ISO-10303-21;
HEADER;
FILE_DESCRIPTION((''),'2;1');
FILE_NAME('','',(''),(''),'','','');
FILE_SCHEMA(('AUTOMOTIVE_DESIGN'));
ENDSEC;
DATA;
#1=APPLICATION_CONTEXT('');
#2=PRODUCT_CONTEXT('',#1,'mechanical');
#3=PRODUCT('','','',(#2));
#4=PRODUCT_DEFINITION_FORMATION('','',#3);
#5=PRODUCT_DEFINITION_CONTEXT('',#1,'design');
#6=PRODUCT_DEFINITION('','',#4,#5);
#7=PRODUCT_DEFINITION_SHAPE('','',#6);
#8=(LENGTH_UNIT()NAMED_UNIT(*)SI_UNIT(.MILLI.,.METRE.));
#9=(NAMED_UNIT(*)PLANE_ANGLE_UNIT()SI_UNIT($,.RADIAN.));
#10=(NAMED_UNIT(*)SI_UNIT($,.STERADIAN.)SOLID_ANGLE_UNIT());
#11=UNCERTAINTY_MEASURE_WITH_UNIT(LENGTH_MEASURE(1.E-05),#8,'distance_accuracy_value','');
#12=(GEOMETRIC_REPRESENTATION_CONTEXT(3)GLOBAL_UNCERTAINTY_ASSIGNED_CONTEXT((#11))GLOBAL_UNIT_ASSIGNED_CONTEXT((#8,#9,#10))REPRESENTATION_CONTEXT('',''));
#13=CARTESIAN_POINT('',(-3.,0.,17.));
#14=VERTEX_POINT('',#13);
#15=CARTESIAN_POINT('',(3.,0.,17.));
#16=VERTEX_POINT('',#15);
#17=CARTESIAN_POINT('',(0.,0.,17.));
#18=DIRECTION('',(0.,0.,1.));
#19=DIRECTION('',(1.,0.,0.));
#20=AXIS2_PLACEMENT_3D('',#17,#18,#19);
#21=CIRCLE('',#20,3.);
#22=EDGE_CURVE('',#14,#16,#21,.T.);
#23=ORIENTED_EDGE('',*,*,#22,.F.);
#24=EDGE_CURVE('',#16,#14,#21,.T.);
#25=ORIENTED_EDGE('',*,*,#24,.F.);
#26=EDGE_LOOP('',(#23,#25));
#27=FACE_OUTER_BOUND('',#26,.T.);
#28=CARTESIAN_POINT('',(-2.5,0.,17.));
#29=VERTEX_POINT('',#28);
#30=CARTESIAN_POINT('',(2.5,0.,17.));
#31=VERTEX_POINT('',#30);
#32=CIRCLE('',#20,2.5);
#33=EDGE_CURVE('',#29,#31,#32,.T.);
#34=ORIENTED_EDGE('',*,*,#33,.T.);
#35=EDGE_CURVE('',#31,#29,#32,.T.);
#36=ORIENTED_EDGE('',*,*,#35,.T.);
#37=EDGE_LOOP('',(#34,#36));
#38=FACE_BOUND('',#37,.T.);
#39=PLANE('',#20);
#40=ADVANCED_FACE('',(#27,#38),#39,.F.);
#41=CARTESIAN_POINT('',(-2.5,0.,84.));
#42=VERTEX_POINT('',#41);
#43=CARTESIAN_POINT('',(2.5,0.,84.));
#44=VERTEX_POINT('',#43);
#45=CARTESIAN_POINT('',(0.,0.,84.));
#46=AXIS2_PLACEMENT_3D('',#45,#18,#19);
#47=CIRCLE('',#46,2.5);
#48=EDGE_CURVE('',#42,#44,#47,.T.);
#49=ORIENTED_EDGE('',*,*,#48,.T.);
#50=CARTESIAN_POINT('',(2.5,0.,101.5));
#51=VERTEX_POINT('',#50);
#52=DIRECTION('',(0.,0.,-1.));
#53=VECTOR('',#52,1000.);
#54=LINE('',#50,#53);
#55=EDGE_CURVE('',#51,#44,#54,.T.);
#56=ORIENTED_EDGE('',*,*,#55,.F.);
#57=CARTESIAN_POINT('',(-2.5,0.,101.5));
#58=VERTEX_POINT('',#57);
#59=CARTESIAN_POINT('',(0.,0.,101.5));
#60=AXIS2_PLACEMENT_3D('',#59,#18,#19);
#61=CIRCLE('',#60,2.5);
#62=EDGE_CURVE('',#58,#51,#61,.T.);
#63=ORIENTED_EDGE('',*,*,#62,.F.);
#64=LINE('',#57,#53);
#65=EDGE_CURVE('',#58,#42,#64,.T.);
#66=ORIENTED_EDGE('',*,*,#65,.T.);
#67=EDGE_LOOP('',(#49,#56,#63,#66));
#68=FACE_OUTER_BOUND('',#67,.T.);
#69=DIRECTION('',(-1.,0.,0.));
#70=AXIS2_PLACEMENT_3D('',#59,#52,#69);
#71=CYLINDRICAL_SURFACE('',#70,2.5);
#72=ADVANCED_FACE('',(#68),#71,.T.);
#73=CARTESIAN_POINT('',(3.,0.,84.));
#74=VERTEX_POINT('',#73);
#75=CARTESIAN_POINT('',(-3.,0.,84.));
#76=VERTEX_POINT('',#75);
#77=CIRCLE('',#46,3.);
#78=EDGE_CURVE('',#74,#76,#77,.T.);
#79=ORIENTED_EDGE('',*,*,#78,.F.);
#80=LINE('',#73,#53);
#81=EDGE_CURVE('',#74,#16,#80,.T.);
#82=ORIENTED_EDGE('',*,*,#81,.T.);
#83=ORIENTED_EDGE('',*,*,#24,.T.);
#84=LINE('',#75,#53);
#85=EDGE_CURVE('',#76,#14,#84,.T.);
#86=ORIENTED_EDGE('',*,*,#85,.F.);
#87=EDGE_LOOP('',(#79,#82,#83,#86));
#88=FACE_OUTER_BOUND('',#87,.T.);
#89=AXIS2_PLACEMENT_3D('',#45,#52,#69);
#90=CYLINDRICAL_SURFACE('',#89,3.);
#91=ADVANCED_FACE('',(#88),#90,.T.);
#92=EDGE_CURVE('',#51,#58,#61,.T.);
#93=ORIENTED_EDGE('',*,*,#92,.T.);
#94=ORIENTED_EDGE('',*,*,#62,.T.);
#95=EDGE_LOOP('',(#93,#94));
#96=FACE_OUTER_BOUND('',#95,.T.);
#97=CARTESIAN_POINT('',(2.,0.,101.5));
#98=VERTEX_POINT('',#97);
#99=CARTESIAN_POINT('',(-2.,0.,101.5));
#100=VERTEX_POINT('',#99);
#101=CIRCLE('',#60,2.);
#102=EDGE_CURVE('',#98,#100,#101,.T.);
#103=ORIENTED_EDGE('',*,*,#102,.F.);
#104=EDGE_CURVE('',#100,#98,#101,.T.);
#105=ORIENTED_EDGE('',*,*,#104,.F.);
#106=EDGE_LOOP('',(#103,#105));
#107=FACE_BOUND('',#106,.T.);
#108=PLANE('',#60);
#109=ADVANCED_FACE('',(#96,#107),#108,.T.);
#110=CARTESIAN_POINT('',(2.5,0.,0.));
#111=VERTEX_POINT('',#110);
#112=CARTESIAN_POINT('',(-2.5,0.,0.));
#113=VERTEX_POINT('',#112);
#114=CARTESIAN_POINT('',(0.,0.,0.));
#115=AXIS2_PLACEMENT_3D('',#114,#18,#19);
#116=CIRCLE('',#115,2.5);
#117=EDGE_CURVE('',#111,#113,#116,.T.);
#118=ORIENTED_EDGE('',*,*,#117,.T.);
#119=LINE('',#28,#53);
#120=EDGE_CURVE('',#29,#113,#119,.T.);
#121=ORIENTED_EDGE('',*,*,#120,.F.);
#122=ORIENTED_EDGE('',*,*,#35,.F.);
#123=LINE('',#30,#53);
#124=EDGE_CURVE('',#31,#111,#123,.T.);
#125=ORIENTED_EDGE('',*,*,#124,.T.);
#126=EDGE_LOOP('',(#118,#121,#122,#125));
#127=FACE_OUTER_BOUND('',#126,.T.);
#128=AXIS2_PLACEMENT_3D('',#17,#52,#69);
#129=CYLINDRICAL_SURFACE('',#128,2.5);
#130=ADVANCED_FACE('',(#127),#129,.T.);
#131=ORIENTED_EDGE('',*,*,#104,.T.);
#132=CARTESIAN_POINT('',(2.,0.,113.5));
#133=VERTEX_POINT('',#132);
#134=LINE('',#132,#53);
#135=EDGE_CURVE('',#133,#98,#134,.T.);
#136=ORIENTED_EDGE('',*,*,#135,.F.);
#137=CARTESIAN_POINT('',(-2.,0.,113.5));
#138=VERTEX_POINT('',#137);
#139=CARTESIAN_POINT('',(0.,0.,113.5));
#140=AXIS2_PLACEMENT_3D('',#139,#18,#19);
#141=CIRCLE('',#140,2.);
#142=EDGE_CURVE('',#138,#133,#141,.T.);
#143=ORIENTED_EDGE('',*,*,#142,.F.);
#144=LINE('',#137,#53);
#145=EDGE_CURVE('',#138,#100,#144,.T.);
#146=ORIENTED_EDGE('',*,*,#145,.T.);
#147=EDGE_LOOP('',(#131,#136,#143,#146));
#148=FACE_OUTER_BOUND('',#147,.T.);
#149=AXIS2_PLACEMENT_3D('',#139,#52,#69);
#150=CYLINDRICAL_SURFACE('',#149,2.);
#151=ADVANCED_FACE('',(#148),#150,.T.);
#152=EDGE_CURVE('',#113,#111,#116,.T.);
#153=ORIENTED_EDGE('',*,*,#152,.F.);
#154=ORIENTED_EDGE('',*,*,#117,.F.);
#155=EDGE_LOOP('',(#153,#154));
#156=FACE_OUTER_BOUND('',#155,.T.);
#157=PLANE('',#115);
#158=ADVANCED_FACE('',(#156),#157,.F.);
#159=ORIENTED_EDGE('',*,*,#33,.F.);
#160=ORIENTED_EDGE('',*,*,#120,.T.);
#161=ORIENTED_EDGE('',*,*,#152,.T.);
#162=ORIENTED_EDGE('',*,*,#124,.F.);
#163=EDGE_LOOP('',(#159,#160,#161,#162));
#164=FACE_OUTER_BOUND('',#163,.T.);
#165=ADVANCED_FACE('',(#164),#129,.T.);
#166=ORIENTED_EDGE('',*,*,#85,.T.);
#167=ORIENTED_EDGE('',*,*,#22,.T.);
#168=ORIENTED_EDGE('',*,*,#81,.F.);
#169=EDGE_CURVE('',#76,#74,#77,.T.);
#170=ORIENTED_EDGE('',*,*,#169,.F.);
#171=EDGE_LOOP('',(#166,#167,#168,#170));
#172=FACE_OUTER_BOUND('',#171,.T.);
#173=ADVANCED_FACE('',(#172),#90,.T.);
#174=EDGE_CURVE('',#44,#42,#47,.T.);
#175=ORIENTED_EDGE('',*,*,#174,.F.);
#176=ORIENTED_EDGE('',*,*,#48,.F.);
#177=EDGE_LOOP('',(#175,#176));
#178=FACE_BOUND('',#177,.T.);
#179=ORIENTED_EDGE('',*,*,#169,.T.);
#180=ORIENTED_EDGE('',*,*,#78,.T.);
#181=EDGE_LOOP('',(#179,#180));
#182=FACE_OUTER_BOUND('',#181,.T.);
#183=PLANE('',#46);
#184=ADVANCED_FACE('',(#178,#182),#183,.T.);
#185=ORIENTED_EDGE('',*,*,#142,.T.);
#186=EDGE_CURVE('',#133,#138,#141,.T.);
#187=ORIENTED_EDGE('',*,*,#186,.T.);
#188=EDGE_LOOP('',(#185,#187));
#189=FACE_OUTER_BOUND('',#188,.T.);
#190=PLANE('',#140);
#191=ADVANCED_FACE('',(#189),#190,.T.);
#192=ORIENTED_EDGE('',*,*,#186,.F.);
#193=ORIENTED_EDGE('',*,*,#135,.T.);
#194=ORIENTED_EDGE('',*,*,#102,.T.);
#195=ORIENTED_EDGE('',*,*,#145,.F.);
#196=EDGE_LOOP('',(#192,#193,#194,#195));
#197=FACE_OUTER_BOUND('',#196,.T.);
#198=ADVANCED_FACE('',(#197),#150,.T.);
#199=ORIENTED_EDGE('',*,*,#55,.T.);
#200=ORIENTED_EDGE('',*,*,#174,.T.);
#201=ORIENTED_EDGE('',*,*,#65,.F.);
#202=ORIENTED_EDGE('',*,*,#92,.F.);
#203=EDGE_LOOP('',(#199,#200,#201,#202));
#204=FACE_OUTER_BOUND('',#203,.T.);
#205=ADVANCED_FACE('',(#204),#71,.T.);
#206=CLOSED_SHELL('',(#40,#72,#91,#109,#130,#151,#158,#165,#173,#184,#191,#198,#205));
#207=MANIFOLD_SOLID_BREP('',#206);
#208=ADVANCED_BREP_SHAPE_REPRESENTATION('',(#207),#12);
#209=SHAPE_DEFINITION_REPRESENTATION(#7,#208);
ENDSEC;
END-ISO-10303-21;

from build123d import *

# Parameters (mm, degrees)
SKETCH1_R           = 2.5
BOSS_EXTRUDE1_DEPTH = 17
SKETCH2_R           = 3
BOSS_EXTRUDE2_DEPTH = 67
SKETCH3_R           = 2.5
BOSS_EXTRUDE3_DEPTH = 17.5
SKETCH4_R           = 2
BOSS_EXTRUDE4_DEPTH = 12


with BuildPart() as part:
    # Sketch1 → Boss-Extrude1 (new body)
    with BuildSketch(Plane.XY):
        Circle(SKETCH1_R)
    extrude(amount=BOSS_EXTRUDE1_DEPTH)

    # Sketch2 → Boss-Extrude2 (add)
    with BuildSketch(Plane.XY.offset(17)):
        Circle(SKETCH2_R)
    extrude(amount=BOSS_EXTRUDE2_DEPTH)

    # Sketch3 → Boss-Extrude3 (add)
    with BuildSketch(Plane.XY.offset(84)):
        Circle(SKETCH3_R)
    extrude(amount=BOSS_EXTRUDE3_DEPTH)

    # Sketch4 → Boss-Extrude4 (add)
    with BuildSketch(Plane.XY.offset(101.5)):
        Circle(SKETCH4_R)
    extrude(amount=BOSS_EXTRUDE4_DEPTH)


solid = part.part
